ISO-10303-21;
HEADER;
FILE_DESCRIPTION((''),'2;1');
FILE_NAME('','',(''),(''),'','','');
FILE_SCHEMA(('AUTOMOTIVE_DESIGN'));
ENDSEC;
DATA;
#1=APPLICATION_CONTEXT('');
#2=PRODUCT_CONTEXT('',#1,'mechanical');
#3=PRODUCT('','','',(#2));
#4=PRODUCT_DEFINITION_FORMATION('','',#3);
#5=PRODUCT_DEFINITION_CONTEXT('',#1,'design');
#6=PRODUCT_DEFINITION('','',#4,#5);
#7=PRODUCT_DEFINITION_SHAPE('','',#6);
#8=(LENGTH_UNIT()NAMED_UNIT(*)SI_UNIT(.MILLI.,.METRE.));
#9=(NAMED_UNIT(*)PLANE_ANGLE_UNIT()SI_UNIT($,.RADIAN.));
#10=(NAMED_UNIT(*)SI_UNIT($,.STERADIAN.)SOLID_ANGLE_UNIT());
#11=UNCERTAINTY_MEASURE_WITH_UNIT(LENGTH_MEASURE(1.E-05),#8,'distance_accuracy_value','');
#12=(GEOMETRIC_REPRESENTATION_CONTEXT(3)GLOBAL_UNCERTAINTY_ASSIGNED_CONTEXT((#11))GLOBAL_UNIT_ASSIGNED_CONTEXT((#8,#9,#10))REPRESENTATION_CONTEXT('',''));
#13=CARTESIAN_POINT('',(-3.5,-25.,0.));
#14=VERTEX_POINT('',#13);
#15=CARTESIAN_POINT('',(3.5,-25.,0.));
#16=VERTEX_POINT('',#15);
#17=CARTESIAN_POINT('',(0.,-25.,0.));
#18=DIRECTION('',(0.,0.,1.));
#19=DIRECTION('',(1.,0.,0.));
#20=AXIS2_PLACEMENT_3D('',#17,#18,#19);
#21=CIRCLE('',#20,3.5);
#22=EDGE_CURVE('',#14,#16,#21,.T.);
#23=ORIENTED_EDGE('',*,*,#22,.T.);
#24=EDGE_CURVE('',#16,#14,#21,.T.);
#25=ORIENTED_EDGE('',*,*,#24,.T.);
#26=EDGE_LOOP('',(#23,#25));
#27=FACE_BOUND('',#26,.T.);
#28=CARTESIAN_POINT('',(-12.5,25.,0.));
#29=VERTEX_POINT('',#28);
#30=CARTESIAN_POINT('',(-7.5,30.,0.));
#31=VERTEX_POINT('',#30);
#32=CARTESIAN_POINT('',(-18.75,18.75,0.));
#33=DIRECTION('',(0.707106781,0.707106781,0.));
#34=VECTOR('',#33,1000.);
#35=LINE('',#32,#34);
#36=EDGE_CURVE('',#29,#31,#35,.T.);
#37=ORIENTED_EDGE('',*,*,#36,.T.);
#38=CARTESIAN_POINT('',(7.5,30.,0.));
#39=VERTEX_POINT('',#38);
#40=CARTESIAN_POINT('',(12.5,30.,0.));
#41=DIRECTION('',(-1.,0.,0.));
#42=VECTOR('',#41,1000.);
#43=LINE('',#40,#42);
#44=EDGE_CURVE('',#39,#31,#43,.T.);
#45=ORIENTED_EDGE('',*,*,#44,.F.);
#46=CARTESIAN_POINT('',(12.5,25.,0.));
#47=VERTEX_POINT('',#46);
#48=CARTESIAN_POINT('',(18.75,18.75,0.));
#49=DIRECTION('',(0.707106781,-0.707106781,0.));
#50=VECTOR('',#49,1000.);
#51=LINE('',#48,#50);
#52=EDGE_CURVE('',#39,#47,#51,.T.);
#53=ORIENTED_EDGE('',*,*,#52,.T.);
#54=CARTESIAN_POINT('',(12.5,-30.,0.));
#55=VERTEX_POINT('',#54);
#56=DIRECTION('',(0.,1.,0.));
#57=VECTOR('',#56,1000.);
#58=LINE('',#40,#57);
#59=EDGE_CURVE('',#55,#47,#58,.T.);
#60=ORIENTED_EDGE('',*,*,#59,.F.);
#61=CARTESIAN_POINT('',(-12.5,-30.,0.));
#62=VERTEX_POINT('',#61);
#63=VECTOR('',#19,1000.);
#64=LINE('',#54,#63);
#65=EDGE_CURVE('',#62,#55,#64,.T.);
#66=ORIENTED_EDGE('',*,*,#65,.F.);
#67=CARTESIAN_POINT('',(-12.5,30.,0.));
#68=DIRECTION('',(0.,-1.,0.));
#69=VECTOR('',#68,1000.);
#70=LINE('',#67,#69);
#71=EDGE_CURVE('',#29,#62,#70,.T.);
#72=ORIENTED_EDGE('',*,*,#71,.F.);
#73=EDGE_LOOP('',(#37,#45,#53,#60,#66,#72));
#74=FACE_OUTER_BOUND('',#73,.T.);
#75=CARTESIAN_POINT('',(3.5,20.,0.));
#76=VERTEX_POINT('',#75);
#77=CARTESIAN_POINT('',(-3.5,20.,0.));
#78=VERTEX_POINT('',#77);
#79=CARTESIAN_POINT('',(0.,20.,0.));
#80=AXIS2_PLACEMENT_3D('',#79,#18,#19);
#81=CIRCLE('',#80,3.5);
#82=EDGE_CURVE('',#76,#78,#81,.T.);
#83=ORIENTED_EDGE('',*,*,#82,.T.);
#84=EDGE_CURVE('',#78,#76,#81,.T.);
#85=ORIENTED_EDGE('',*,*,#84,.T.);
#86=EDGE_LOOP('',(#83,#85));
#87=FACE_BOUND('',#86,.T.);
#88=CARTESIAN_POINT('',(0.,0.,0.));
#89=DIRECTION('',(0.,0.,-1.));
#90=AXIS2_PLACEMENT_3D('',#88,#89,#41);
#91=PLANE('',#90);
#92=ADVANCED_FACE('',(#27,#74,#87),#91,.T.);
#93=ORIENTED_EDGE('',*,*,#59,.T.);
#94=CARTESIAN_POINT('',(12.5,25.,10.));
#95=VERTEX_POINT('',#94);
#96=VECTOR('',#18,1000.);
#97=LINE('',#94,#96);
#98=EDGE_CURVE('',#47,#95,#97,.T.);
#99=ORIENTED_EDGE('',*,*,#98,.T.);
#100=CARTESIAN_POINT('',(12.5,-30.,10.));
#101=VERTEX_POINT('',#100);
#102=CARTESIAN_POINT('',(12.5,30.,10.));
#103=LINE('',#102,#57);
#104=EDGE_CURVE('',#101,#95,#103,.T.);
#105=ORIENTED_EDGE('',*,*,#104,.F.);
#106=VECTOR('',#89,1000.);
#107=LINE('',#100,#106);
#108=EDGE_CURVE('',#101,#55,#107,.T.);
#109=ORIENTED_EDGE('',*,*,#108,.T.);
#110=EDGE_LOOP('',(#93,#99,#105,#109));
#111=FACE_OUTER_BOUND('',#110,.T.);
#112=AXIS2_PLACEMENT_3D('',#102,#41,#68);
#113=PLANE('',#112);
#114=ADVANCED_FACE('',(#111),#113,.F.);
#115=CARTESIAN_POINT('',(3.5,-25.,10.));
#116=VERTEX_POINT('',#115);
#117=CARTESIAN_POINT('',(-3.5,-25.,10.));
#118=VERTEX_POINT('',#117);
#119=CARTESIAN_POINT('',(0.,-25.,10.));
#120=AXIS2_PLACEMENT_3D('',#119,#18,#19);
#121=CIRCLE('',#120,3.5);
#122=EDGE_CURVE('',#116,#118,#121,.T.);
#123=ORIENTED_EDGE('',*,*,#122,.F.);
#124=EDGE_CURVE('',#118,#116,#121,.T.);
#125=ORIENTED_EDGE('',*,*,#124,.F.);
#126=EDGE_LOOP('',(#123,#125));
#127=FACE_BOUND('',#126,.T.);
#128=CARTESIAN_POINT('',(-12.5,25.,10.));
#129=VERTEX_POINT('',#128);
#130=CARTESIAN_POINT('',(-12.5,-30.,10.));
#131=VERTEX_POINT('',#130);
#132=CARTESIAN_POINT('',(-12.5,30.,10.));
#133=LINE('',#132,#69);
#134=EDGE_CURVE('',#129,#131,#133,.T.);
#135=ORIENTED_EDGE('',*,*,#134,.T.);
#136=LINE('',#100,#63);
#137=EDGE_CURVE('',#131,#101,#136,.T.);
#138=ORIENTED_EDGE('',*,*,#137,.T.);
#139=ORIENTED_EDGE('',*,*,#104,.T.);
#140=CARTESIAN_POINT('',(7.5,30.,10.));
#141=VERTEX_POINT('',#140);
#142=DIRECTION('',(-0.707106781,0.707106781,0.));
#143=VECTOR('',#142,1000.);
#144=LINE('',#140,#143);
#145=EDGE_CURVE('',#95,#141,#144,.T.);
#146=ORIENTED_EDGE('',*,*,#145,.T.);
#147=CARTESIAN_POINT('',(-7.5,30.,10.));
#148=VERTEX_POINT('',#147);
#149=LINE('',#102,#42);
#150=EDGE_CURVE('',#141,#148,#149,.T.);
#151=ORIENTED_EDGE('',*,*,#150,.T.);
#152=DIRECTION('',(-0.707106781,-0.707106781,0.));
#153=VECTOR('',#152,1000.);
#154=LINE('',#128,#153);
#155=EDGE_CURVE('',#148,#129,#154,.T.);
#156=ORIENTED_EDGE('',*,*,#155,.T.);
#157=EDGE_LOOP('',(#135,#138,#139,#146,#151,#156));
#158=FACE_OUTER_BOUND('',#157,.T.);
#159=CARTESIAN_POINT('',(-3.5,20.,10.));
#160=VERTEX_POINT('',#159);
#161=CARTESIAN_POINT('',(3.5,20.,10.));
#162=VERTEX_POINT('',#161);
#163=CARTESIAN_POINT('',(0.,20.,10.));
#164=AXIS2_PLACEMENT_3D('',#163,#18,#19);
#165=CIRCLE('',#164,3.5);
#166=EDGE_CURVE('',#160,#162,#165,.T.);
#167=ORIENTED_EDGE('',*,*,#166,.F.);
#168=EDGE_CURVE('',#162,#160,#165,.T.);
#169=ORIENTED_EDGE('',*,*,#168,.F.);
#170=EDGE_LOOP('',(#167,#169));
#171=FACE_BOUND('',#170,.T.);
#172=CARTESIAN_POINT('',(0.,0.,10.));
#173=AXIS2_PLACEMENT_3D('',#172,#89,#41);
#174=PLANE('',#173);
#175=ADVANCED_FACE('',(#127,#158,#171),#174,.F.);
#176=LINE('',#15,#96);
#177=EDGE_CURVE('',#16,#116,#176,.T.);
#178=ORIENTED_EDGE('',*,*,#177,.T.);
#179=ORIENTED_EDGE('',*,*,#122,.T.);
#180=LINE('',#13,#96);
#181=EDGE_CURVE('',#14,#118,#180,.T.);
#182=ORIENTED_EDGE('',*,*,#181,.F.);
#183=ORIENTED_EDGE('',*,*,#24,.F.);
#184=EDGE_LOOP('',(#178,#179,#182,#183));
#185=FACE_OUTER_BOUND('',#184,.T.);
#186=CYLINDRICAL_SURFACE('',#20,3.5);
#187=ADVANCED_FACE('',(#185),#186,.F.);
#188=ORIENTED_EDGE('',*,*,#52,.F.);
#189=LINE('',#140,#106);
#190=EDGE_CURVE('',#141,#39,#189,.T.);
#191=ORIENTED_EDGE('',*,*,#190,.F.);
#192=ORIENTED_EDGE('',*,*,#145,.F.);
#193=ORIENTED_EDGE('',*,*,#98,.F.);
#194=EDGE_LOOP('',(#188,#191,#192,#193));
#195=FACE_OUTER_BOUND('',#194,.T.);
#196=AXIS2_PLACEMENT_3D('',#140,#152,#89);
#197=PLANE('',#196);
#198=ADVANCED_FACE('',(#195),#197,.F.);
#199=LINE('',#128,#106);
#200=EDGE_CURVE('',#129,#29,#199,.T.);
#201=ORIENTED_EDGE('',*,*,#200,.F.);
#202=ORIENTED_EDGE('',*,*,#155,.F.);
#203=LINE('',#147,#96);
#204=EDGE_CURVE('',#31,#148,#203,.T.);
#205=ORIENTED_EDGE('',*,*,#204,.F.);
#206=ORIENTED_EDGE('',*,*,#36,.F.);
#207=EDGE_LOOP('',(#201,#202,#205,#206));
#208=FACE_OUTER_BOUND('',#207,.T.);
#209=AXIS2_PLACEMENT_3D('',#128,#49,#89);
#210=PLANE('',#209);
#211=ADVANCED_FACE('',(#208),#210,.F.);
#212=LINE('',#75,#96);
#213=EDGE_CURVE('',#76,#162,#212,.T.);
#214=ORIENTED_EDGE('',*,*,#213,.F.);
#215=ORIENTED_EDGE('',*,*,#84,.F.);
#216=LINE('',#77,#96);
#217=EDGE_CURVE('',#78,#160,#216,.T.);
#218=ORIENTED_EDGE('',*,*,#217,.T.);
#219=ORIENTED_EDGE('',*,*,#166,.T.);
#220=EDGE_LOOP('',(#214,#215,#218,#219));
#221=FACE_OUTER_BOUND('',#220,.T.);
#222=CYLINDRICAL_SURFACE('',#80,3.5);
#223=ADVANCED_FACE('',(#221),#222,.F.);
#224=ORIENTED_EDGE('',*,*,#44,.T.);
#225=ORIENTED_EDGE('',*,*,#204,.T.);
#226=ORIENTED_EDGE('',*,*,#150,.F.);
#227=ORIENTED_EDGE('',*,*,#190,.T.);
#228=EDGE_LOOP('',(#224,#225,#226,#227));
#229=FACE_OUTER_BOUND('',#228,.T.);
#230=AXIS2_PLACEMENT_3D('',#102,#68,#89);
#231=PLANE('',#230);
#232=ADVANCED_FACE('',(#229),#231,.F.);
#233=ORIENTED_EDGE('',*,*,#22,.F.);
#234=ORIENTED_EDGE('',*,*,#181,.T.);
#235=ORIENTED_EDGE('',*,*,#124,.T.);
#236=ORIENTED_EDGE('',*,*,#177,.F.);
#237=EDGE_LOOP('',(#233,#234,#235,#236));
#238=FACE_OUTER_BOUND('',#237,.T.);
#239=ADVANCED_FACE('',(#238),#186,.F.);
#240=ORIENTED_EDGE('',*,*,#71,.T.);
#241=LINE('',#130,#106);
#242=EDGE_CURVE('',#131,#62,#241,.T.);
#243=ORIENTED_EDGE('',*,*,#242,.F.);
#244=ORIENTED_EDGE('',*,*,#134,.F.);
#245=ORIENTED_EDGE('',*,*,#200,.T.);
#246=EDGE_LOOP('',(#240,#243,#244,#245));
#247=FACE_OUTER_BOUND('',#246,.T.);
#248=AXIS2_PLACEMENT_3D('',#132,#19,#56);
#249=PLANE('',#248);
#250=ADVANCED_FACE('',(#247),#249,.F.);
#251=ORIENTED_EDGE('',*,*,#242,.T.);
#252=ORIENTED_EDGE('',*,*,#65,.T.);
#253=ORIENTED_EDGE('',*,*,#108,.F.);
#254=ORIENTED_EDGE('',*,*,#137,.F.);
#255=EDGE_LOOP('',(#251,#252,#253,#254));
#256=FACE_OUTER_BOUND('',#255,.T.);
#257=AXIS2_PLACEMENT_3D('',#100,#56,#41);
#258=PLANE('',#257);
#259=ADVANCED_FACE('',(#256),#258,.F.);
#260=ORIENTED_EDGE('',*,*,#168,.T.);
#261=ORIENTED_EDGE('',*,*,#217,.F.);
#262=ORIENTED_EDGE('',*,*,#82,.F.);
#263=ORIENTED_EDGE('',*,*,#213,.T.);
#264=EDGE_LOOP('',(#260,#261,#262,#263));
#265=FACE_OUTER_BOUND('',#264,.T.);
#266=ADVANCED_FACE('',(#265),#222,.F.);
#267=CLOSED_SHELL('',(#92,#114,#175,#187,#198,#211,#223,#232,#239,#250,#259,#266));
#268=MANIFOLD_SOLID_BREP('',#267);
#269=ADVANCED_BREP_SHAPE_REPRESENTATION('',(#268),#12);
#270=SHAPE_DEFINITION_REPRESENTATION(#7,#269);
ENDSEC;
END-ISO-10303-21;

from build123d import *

# Parameters (mm, degrees)
SKETCH1_W           = 25
SKETCH1_H           = 60
BOSS_EXTRUDE1_DEPTH = 10
SKETCH2_R           = 3.5
CUT_EXTRUDE1_DEPTH  = 10
CHAMFER1_SIZE       = 5


with BuildPart() as part:
    # Sketch1 → Boss-Extrude1 (new body)
    with BuildSketch(Plane.XY):
        Rectangle(SKETCH1_W, SKETCH1_H)
    extrude(amount=BOSS_EXTRUDE1_DEPTH)

    # Sketch2 → Cut-Extrude1 (cut)
    with BuildSketch(Plane.XY.offset(10)):
        with Locations((0, 20)):
            Circle(SKETCH2_R)
        with Locations((0, -25)):
            Circle(SKETCH2_R)
    extrude(amount=-CUT_EXTRUDE1_DEPTH, mode=Mode.SUBTRACT)

    # Chamfer1
    chamfer1_edges = [part.edges().sort_by_distance(p)[0] for p in [
        (-12.5, 30, 5),
        (12.5, 30, 5),
    ]]
    chamfer(chamfer1_edges, length=CHAMFER1_SIZE)


solid = part.part
